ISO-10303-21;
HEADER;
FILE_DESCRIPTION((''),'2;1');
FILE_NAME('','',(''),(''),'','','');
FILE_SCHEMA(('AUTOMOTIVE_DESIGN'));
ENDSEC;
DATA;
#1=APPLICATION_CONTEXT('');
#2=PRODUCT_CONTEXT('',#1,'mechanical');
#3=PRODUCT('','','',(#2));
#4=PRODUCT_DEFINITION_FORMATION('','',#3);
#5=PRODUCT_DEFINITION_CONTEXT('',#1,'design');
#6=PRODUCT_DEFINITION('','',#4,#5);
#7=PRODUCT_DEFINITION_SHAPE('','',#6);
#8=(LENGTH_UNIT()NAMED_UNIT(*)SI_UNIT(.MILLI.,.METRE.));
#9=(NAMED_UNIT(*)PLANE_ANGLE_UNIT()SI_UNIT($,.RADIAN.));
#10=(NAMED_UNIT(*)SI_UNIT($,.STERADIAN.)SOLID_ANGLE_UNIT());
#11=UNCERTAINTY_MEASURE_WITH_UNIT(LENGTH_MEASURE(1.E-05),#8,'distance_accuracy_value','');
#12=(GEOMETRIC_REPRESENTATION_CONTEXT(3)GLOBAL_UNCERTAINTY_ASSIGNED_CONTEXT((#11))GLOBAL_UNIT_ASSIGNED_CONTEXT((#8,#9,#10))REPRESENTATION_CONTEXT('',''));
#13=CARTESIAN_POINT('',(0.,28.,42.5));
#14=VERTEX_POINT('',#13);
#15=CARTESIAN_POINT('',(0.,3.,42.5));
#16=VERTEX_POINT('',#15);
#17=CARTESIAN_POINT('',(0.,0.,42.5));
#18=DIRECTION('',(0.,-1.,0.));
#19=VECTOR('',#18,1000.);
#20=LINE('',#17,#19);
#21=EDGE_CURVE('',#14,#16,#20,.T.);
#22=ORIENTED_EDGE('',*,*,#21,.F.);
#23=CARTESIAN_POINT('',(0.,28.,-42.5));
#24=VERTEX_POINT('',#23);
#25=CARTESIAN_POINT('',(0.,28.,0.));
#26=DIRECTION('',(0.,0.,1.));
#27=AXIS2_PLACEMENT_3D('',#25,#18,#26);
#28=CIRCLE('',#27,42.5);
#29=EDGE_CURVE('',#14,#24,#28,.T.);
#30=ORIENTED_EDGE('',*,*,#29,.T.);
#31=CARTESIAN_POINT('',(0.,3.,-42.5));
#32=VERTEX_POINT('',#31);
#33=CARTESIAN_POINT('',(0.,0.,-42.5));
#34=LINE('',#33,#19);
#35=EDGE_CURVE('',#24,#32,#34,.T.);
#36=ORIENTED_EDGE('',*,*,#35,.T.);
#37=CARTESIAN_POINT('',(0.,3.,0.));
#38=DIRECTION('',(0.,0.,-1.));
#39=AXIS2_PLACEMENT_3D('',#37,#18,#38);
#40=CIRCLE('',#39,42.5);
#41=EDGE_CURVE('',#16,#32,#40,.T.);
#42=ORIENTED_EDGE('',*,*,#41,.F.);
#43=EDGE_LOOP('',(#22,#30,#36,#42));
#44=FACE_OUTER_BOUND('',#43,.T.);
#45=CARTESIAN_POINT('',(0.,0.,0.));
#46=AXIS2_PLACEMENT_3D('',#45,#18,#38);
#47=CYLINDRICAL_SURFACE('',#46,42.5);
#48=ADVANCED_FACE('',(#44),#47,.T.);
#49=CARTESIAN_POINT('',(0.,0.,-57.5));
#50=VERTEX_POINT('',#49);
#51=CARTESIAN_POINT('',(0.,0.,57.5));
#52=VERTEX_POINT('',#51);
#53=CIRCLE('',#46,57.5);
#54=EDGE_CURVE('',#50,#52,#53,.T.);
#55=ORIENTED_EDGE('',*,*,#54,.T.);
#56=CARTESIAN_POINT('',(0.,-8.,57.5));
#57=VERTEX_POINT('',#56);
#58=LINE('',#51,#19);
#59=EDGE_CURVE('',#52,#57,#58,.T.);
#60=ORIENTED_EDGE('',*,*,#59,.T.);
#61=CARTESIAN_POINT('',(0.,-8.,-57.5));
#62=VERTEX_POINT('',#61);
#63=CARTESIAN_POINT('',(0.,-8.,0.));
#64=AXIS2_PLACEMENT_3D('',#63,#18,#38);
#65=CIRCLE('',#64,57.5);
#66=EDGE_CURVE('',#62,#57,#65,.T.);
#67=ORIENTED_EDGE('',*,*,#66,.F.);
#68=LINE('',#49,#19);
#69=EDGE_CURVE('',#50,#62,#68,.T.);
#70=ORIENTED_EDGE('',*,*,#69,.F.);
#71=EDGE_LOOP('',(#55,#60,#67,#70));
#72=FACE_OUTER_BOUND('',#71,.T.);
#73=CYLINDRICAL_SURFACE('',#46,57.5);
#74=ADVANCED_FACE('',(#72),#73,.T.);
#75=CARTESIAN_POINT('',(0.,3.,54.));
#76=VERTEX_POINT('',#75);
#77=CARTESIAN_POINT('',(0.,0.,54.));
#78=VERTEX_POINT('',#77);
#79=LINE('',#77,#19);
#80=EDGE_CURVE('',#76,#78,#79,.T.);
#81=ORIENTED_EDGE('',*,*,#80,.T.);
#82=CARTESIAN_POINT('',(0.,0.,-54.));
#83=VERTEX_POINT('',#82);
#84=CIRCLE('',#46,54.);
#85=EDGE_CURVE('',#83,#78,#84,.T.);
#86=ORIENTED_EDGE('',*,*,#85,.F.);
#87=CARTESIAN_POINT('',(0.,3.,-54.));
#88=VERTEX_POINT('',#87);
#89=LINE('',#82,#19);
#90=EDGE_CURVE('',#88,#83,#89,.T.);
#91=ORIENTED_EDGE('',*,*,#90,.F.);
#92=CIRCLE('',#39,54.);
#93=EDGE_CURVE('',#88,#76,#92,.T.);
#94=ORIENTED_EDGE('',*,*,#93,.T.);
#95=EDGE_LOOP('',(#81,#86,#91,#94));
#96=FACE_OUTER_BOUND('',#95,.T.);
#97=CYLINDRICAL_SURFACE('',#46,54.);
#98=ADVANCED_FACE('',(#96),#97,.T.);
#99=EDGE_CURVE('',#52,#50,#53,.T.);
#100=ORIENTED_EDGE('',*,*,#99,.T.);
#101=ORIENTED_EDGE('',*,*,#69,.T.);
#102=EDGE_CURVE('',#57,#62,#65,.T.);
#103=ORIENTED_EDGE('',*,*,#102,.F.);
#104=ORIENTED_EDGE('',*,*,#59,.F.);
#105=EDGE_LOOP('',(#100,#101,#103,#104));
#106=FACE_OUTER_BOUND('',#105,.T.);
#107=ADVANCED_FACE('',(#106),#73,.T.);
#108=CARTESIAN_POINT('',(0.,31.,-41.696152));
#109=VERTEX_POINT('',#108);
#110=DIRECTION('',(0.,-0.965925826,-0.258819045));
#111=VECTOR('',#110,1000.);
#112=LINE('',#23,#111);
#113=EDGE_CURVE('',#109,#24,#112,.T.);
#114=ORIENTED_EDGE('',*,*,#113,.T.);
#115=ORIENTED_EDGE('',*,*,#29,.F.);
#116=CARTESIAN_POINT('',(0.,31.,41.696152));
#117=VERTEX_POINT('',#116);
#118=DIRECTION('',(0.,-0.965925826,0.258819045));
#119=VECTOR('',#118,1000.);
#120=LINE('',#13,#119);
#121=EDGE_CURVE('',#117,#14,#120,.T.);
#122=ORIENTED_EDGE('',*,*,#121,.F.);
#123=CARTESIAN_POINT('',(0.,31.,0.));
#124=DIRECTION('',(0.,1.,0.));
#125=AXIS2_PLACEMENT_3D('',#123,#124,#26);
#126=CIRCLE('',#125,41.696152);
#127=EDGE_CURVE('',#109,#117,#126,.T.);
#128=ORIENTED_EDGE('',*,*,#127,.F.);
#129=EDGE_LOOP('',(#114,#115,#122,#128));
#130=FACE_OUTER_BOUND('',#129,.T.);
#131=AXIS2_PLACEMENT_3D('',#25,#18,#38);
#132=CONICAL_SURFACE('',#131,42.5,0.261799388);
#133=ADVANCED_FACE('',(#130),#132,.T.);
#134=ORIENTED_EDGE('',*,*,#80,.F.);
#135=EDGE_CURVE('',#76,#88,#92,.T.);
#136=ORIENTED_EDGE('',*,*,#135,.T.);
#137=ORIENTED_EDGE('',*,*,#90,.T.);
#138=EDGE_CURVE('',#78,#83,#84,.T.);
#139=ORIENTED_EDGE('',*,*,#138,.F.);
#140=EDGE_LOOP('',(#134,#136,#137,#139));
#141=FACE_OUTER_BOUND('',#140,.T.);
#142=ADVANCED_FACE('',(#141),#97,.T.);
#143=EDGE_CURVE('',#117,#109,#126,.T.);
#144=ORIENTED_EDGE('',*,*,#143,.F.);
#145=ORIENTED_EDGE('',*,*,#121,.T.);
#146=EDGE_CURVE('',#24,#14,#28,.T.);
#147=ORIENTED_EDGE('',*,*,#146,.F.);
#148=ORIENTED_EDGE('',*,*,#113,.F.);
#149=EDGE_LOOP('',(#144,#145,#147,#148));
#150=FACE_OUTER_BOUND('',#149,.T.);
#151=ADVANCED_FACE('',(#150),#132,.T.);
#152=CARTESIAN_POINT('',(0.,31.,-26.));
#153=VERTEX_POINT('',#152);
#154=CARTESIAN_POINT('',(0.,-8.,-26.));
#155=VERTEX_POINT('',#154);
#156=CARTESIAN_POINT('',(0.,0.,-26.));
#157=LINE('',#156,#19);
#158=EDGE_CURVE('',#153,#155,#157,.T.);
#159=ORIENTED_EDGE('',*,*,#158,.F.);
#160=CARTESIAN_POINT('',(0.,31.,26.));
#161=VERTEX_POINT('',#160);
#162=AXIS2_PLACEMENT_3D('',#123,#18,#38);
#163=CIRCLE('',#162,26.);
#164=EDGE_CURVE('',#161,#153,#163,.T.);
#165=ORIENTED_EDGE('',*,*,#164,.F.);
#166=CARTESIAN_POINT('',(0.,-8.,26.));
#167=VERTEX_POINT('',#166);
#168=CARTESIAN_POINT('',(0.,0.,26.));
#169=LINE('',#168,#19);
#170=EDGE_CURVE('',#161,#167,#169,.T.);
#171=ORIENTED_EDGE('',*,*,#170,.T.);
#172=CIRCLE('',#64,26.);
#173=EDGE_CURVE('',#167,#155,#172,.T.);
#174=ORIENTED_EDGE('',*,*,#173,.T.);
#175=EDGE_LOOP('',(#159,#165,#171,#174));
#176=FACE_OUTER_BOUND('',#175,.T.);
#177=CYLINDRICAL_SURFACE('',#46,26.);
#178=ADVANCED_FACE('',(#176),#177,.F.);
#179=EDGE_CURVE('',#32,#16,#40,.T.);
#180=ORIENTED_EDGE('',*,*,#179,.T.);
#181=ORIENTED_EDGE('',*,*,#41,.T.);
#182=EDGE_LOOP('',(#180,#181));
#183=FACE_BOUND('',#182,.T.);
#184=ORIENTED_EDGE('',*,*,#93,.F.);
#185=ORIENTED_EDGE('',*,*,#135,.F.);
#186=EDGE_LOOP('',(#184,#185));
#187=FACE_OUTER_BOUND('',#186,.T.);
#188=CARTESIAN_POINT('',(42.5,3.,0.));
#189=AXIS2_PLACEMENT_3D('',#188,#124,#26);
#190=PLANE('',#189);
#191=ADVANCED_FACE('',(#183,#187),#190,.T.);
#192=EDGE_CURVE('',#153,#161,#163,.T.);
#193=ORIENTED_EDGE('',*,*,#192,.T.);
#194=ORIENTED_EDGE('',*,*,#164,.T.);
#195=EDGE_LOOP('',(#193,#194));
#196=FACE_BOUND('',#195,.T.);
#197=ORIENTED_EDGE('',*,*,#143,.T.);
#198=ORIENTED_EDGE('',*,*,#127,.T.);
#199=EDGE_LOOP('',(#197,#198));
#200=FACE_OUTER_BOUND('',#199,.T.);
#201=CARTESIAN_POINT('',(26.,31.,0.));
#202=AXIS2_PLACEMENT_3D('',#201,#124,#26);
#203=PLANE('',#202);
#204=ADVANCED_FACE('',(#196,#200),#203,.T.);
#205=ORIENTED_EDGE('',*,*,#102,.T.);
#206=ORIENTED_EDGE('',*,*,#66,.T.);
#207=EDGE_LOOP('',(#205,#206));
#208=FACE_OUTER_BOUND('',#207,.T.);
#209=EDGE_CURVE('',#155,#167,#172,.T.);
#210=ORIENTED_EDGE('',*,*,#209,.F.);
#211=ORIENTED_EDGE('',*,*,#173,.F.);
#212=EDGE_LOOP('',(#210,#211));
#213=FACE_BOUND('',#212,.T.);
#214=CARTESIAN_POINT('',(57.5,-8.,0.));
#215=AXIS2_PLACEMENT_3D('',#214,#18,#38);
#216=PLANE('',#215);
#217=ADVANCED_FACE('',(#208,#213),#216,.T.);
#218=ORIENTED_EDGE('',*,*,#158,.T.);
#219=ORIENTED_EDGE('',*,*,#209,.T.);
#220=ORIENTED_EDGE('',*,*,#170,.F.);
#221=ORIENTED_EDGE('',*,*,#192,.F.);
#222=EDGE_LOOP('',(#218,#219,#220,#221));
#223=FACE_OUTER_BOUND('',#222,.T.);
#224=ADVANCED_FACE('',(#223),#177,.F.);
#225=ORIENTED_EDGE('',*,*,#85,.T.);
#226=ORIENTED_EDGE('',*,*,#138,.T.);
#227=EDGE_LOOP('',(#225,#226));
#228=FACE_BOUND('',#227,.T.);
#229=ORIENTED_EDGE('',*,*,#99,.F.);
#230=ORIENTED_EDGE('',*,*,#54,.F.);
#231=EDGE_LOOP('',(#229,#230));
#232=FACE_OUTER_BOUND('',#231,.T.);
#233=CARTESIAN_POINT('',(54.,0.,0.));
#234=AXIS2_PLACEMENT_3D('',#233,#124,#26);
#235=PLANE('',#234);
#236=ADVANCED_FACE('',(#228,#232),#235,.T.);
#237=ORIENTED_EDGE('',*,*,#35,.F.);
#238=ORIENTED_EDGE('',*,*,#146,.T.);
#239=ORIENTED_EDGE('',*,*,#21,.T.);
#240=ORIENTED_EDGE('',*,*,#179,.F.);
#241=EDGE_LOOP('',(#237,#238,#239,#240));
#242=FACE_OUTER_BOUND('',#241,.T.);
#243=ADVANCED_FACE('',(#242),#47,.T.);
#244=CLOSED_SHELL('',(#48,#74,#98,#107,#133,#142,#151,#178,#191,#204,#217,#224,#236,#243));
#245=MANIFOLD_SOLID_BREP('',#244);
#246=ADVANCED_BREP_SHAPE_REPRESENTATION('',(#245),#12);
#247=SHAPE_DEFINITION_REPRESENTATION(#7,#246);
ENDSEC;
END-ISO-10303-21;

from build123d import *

# Parameters (mm, degrees)
CHAMFER1_SIZE  = 3
CHAMFER1_SIZE2 = 0.803847577


with BuildPart() as part:
    # Sketch1 → Revolve1 (revolve)
    with BuildSketch(Plane.XY, mode=Mode.PRIVATE) as revolve1_sk:
        Polygon((26, 31), (42.5, 31), (42.5, 3), (54, 3), (54, 0), (57.5, 0), (57.5, -8), (26, -8), align=None)
    revolve(revolve1_sk.sketch.rotate(Axis((0, 0, 0), (0, 1, 0)), 90), axis=Axis((0, 0, 0), (0, 1, 0)))

    # Chamfer1
    chamfer1_edges = [part.edges().sort_by_distance(p)[0] for p in [
        (0, 31, 42.5),
    ]]
    chamfer1_side = [part.faces().sort_by_distance(p)[0] for p in [
        (0, 17, 42.5),
    ]]
    chamfer(chamfer1_edges, length=CHAMFER1_SIZE, length2=CHAMFER1_SIZE2, reference=chamfer1_side[0])


solid = part.part
